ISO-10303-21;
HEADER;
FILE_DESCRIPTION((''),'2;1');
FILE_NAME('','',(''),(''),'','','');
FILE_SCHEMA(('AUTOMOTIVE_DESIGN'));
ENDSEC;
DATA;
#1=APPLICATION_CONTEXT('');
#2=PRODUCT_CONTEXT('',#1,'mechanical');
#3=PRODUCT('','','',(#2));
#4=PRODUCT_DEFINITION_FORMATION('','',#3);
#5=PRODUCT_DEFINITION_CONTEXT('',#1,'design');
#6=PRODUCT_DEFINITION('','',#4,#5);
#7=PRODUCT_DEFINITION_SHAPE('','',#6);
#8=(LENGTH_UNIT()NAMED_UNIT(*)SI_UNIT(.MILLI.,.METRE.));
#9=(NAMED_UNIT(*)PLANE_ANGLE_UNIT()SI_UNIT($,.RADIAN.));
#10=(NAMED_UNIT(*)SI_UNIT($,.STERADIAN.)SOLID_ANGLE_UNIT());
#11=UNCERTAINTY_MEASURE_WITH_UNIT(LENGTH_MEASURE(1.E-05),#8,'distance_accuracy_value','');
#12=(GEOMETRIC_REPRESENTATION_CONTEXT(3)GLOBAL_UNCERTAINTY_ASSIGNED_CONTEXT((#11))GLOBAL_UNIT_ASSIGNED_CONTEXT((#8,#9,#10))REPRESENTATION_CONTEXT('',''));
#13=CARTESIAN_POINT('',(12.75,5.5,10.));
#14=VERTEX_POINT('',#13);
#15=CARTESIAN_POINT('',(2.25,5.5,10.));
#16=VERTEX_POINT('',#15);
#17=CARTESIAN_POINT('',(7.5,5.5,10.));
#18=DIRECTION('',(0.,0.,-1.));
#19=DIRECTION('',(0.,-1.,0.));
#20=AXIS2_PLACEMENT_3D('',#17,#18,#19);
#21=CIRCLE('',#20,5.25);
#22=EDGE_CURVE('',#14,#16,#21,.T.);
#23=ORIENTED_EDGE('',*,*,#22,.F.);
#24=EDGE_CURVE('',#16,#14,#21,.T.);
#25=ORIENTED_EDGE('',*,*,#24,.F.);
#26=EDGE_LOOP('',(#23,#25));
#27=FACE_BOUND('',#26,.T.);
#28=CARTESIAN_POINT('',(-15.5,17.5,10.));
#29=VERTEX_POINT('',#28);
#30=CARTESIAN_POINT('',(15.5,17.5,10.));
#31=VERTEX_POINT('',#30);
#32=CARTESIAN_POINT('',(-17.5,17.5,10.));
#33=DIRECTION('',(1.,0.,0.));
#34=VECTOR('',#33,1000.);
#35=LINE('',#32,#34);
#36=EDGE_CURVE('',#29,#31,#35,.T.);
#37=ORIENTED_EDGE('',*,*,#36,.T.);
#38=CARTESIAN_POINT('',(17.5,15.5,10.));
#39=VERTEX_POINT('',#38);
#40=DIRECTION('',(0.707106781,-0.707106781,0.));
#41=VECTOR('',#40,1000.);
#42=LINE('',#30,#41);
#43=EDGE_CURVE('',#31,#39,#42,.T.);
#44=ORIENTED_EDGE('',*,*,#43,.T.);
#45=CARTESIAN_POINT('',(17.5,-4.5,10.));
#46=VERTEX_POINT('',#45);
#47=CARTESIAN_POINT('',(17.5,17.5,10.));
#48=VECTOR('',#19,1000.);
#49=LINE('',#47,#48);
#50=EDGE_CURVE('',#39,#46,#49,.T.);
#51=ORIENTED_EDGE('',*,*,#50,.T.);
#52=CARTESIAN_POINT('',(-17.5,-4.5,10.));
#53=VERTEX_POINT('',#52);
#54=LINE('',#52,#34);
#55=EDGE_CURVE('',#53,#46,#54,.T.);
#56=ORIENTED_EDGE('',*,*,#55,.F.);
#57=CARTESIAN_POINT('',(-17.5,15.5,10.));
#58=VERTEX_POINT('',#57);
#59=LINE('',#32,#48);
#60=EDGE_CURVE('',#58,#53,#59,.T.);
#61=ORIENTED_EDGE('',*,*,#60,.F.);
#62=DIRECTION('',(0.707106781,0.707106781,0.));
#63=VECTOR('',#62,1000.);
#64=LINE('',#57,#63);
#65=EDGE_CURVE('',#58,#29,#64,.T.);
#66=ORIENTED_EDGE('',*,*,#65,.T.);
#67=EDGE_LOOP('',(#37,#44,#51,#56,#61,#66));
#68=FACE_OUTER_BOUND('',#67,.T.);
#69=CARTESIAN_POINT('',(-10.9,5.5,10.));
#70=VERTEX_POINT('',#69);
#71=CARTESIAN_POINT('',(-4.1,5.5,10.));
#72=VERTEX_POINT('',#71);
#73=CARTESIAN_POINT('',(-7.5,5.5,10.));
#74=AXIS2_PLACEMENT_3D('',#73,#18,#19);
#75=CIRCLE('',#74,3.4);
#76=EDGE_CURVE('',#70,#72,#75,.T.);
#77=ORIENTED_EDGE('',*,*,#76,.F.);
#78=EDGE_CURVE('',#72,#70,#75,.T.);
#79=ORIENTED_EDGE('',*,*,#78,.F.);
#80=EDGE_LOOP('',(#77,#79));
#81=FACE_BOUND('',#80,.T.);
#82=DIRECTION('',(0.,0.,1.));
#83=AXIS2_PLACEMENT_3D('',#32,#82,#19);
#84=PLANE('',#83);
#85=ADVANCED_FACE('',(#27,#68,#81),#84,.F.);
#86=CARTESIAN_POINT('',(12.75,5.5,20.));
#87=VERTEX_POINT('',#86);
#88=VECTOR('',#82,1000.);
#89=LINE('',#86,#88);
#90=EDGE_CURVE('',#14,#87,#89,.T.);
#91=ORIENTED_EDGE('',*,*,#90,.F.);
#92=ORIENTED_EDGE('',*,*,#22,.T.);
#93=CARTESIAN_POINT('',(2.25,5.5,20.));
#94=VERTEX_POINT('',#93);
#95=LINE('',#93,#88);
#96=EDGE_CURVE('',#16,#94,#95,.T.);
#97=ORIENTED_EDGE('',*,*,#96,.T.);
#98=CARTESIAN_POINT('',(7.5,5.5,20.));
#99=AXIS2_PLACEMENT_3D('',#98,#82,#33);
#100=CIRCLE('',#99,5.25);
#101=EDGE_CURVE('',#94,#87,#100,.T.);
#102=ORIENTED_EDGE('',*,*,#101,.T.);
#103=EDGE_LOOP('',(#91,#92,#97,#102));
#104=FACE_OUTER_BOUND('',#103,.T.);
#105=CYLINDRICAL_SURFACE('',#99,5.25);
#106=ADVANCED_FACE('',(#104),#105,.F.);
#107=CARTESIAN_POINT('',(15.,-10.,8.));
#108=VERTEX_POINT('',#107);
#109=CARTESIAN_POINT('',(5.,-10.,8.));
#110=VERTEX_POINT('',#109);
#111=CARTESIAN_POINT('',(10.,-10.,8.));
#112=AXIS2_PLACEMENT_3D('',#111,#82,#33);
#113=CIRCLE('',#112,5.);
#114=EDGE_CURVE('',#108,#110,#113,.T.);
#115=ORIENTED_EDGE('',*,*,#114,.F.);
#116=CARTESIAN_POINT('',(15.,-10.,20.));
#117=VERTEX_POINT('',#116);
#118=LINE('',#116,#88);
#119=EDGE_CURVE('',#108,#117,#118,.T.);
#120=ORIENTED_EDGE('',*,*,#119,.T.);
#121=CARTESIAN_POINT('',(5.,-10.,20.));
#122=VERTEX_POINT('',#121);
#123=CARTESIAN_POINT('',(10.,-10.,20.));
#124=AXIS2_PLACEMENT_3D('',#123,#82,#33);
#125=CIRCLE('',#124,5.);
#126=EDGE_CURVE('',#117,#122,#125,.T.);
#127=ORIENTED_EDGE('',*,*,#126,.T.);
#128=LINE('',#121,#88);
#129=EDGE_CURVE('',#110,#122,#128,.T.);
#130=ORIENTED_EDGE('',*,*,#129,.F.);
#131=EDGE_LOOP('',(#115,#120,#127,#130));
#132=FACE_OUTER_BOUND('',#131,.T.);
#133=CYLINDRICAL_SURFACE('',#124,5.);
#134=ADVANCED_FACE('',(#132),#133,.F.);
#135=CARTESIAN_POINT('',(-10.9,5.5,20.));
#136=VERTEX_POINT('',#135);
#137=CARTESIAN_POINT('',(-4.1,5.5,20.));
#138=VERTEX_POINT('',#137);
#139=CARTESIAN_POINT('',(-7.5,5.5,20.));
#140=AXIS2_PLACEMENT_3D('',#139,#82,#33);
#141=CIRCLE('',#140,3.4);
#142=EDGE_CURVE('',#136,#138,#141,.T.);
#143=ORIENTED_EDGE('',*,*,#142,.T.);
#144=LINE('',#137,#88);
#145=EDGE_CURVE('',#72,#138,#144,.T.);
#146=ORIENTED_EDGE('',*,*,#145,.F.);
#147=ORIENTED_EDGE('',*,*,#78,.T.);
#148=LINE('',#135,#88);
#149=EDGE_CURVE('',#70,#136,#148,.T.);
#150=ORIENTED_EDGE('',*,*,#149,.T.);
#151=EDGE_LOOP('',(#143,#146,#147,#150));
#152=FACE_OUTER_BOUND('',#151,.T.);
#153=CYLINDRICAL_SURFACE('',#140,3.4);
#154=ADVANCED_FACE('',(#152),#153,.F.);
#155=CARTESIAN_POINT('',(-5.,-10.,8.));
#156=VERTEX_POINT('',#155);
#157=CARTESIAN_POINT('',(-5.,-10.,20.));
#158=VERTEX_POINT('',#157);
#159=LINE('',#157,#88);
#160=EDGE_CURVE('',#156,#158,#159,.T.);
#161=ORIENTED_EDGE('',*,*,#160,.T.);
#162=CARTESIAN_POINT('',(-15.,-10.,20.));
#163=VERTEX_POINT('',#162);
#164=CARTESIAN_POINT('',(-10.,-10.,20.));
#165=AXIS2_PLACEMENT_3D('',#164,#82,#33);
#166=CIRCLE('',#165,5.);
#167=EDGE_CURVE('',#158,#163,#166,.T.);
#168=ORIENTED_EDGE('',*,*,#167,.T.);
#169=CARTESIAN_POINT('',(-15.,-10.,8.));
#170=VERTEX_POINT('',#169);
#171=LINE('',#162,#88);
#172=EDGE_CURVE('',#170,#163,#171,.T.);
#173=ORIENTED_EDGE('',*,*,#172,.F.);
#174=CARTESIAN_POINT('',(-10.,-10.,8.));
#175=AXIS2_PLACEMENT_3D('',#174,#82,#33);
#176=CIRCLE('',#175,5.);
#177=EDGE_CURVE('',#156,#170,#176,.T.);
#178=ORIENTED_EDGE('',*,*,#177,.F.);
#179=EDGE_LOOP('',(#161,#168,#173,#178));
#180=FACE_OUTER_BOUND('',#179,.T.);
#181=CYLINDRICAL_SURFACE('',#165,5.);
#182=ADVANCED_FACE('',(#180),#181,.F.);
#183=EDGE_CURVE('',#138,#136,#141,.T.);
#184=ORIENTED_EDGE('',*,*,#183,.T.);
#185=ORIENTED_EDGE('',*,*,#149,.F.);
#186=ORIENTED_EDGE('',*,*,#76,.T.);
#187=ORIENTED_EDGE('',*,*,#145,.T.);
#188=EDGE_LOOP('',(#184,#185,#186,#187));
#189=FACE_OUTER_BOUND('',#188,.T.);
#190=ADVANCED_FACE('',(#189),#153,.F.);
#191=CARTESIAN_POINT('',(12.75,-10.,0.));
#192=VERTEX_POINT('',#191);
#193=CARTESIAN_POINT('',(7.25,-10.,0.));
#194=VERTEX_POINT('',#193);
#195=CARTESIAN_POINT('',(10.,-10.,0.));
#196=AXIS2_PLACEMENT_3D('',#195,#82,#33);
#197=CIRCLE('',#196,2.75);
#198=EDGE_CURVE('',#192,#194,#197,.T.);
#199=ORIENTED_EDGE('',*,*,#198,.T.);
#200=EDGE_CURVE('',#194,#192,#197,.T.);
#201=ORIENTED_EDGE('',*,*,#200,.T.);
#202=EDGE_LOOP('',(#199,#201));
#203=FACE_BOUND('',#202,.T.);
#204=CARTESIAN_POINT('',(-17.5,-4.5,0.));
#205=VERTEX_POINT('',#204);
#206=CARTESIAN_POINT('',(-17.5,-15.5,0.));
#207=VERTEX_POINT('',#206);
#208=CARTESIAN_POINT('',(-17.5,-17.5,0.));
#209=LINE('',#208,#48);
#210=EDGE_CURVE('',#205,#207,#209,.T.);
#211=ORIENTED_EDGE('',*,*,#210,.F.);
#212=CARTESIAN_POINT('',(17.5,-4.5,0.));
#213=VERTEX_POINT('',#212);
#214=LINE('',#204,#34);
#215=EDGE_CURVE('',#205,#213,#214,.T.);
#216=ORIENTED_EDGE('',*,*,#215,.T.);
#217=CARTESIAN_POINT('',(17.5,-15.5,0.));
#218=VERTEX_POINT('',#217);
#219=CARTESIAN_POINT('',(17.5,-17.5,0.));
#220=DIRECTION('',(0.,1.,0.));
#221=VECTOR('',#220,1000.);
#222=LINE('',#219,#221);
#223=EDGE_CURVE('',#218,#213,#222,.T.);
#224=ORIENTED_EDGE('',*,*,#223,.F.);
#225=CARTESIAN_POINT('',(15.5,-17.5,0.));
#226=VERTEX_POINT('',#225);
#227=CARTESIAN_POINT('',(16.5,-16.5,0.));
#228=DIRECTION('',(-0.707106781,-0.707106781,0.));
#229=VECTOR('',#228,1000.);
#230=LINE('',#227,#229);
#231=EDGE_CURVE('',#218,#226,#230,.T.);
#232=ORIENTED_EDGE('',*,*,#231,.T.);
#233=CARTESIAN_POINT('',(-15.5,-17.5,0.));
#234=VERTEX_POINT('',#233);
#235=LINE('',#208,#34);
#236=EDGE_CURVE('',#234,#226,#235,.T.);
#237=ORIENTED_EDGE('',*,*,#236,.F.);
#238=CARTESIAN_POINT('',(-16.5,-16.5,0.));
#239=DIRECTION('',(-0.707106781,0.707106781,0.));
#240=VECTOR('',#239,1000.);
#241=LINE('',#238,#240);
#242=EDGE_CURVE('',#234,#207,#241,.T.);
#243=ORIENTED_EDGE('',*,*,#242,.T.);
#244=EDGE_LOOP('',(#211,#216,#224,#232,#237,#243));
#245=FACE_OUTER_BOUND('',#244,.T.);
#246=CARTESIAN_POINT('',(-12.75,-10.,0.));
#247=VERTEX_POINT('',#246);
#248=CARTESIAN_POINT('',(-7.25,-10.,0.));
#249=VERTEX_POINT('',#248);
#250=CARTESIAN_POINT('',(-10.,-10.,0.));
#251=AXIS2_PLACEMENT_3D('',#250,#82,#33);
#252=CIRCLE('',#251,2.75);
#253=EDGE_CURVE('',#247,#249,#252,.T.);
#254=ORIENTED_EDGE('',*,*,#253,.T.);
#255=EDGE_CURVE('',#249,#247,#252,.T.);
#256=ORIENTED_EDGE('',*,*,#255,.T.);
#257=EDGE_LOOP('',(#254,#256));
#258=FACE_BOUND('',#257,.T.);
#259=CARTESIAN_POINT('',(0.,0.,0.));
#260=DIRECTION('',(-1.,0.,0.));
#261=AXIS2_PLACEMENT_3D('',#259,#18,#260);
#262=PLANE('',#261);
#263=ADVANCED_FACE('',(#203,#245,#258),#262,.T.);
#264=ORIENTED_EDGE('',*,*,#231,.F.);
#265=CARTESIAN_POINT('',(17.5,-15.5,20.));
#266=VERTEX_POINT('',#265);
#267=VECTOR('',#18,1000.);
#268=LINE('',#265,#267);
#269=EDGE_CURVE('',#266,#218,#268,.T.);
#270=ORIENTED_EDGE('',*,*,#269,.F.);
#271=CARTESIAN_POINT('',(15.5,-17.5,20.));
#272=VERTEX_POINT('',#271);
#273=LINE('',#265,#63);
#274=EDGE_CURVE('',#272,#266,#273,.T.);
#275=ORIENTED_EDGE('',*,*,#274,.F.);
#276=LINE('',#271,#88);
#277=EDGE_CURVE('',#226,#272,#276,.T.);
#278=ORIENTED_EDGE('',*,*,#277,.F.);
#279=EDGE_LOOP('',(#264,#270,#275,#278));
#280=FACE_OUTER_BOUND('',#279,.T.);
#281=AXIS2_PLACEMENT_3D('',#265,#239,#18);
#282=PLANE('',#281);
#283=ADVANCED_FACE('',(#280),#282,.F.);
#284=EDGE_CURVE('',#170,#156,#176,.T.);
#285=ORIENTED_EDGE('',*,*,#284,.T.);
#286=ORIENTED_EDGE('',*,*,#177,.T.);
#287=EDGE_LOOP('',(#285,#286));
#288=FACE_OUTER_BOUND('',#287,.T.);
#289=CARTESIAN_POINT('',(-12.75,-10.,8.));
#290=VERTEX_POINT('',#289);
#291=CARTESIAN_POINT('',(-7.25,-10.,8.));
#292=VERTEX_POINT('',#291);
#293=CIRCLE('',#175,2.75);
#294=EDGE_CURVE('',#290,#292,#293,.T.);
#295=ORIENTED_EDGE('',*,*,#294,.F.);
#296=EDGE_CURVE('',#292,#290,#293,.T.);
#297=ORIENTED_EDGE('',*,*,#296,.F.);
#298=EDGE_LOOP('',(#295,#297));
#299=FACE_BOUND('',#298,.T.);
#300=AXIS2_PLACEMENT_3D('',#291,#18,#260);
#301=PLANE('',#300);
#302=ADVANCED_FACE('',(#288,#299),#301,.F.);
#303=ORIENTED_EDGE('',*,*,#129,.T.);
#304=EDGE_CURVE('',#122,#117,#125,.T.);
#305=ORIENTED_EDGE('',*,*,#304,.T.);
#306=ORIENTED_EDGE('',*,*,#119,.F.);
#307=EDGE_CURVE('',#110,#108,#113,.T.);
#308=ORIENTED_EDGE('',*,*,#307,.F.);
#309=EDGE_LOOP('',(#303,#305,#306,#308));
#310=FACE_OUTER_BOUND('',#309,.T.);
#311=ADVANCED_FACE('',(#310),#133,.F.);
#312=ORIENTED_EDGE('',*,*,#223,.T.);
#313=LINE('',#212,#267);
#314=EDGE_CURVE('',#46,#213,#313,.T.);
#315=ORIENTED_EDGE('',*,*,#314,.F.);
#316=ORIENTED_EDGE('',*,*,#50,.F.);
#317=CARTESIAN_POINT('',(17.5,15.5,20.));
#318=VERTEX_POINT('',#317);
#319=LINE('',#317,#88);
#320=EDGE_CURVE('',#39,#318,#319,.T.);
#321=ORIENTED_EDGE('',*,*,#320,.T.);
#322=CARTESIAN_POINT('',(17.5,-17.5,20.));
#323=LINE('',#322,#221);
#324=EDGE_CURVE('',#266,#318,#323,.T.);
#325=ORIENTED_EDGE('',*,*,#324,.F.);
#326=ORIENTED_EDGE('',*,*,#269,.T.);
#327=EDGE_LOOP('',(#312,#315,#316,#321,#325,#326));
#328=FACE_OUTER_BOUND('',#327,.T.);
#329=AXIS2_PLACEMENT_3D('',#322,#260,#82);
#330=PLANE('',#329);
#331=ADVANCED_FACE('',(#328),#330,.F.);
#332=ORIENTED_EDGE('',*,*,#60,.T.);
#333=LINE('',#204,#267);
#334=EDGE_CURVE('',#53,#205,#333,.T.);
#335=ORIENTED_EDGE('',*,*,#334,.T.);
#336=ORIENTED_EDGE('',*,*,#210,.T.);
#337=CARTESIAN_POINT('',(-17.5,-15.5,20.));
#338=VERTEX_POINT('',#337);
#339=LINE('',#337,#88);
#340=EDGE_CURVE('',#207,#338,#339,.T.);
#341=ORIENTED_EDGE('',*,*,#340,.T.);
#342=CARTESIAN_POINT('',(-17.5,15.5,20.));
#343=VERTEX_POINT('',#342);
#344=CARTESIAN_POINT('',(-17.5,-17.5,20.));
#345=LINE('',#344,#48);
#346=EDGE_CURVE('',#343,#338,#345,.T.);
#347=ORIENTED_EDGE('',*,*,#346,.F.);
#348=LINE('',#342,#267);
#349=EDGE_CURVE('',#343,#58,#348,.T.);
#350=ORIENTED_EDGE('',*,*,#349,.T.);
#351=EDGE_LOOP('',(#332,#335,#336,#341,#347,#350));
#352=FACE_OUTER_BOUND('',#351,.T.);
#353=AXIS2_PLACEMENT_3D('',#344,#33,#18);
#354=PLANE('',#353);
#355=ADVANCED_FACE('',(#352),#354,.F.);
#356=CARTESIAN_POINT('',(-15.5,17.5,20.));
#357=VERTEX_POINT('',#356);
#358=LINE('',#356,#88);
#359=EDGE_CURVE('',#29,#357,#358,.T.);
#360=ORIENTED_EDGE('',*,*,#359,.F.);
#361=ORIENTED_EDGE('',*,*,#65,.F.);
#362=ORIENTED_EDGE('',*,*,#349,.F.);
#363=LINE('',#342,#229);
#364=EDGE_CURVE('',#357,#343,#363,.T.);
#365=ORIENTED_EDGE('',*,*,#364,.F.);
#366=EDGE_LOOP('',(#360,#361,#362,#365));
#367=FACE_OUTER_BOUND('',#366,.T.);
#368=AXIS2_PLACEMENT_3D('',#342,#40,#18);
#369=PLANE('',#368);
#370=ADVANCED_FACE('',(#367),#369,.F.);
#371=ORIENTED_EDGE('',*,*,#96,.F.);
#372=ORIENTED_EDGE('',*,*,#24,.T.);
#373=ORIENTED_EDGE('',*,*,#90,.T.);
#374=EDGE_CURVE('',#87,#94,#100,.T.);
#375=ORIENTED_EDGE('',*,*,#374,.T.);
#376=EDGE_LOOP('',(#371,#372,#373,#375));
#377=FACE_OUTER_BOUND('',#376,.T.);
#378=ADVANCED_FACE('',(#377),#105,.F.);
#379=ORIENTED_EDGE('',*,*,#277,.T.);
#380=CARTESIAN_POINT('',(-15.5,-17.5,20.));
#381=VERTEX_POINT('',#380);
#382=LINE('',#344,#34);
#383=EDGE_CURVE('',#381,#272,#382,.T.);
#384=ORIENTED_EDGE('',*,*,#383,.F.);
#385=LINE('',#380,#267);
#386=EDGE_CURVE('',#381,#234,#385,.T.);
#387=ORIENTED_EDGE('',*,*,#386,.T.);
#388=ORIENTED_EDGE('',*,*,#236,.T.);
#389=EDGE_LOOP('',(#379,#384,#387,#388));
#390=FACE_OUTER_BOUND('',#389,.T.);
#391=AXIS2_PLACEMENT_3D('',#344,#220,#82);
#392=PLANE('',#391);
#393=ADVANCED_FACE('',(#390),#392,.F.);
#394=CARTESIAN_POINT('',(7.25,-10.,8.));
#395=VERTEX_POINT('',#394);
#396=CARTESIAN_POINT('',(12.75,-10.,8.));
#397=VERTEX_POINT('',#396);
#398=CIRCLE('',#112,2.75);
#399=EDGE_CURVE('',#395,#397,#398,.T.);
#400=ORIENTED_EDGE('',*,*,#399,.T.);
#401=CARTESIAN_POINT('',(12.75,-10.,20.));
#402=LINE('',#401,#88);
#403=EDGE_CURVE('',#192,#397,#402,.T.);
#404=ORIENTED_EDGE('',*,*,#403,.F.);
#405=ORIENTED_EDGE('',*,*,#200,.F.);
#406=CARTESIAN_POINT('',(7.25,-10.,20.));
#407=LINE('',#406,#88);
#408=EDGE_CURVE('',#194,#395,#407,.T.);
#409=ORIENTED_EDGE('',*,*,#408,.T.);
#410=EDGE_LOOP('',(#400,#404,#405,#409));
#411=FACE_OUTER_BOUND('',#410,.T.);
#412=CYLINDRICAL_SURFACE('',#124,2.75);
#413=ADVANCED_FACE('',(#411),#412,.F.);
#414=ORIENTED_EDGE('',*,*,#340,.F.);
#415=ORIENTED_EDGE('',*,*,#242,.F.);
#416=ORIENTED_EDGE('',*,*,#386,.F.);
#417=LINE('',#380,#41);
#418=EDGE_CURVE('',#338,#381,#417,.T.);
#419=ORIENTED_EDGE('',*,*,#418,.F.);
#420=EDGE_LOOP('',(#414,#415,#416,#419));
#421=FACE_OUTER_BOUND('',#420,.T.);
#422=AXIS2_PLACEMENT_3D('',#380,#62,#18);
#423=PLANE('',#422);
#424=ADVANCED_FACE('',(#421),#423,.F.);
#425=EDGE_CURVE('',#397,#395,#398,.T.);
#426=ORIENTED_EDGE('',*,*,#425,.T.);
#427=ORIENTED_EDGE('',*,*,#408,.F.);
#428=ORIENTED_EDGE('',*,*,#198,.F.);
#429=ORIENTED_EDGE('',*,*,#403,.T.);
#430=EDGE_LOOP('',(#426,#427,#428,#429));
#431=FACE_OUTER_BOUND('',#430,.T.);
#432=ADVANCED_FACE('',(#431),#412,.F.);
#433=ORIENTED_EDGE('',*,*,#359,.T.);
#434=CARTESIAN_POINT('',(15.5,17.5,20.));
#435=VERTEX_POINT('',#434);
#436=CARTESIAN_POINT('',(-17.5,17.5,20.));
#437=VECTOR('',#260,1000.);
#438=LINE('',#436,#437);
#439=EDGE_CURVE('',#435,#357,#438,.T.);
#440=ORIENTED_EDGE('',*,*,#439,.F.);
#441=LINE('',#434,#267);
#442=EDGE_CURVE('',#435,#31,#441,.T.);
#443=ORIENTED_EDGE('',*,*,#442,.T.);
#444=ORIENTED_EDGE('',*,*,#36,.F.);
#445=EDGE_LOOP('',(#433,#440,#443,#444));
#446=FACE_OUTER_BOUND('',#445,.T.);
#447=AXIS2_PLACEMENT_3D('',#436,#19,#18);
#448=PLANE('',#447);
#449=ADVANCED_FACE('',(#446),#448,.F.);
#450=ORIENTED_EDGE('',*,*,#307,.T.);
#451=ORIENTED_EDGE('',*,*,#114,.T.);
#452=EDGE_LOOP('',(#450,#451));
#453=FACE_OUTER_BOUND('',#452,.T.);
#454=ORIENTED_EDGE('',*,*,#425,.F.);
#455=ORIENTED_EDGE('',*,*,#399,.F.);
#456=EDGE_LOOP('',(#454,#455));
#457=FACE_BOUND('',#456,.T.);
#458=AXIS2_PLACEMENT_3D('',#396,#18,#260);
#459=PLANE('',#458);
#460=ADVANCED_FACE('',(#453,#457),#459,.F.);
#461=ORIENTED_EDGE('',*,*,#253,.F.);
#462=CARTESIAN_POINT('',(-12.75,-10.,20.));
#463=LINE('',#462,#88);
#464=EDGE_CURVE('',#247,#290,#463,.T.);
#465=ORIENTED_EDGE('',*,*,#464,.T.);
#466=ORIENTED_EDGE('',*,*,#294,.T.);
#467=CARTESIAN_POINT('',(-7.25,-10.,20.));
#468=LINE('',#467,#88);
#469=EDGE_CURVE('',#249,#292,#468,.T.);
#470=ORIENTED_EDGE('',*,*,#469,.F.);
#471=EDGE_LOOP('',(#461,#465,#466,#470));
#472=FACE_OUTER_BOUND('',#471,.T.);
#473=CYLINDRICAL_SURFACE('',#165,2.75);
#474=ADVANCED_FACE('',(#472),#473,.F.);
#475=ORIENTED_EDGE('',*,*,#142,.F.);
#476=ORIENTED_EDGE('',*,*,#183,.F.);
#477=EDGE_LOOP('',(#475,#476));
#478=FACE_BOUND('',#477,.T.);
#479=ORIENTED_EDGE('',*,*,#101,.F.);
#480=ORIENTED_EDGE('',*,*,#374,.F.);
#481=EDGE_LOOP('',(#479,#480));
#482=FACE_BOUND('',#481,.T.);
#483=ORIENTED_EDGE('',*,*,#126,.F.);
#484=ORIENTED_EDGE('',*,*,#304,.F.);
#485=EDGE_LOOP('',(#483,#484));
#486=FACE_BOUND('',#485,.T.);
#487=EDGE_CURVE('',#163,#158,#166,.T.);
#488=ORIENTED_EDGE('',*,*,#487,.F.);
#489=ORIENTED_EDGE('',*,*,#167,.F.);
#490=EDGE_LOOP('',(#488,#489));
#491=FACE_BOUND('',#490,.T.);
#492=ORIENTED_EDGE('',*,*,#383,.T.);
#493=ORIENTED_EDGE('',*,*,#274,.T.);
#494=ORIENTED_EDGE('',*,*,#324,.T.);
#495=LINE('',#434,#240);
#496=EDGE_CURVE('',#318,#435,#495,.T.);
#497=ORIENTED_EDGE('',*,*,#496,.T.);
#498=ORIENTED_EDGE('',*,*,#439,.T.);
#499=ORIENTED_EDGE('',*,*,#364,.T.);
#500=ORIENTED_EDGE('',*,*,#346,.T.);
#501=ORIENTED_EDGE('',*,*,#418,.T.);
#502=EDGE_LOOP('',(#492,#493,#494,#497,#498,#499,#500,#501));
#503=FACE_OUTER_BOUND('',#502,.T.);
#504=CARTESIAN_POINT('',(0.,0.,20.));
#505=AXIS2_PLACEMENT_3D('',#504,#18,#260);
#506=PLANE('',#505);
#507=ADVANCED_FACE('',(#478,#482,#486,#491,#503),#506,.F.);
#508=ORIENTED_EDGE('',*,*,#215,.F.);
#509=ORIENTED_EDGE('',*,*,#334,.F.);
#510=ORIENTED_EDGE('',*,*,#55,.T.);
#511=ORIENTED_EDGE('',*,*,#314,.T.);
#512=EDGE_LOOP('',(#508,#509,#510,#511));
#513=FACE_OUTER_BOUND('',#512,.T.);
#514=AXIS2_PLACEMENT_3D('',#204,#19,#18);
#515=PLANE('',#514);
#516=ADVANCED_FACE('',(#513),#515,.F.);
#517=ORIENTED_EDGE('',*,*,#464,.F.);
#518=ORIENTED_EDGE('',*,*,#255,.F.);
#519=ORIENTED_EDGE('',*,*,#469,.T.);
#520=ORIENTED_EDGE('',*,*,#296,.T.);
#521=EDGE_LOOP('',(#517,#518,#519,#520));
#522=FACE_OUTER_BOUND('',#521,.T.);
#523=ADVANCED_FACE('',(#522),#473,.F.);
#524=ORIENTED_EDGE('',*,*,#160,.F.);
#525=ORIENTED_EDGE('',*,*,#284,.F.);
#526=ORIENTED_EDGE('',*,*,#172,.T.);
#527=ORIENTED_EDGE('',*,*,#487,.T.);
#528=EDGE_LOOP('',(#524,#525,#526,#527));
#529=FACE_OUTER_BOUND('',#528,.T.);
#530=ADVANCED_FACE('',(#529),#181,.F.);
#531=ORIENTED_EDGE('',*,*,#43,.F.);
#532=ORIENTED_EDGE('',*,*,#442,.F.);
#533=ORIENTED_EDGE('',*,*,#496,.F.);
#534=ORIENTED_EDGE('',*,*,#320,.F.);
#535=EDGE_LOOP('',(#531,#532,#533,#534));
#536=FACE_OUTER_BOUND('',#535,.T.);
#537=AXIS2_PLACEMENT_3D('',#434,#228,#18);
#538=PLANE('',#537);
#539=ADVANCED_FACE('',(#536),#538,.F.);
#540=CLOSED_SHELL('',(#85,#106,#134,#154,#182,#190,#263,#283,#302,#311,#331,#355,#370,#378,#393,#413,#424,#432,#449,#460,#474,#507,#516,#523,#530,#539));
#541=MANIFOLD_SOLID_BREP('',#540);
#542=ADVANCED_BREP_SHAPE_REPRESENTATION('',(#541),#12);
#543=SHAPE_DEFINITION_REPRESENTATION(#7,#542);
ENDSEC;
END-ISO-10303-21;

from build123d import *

# Parameters (mm, degrees)
SKETCH_1_W                   = 35
SKETCH_1_H                   = 35
EXTRUDE_1_DEPTH              = 20
CHAMFER_1_SIZE               = 2
M12X1_25_1_D                 = 10.5
HOLE_WIZARD_M8_1_D           = 6.8
HOLE_WIZARD_M5_1_D           = 5.5
HOLE_WIZARD_M5_1_CBORE_D     = 10
HOLE_WIZARD_M5_1_CBORE_DEPTH = 12
SKETCH_11_W                  = 10
SKETCH_11_H                  = 22
CUT_EXTRUDE_1_DEPTH          = 44.945989578


with BuildPart() as part:
    # 草图1 → 凸台-拉伸1 (new body)
    with BuildSketch(Plane.XY):
        Rectangle(SKETCH_1_W, SKETCH_1_H)
    extrude(amount=EXTRUDE_1_DEPTH)

    # 倒角1
    chamfer_1_edges = [part.edges().sort_by_distance(p)[0] for p in [
        (17.5, -17.5, 10),
        (-17.5, -17.5, 10),
        (-17.5, 17.5, 10),
        (17.5, 17.5, 10),
    ]]
    chamfer(chamfer_1_edges, length=CHAMFER_1_SIZE)

    # M12x1.25 螺纹孔1 (through all)
    with Locations(Plane.XY.offset(20)):
        with Locations((7.5, 5.5)):
            Hole(M12X1_25_1_D / 2)

    # M8 螺纹孔1 (through all)
    with Locations(Plane.XY.offset(20)):
        with Locations((-7.5, 5.5)):
            Hole(HOLE_WIZARD_M8_1_D / 2)

    # M5 六角圆柱头螺钉的柱形沉头孔1 (through all)
    with Locations(Plane.XY.offset(20)):
        with Locations((-10, -10), (10, -10)):
            CounterBoreHole(HOLE_WIZARD_M5_1_D / 2, HOLE_WIZARD_M5_1_CBORE_D / 2, HOLE_WIZARD_M5_1_CBORE_DEPTH)

    # 草图11 → 切除-拉伸1 (cut, through all)
    with BuildSketch(Plane(origin=(17.5, 0, 0), x_dir=(0, 0, -1), z_dir=(1, 0, 0))):
        with Locations((-5, 6.5)):
            Rectangle(SKETCH_11_W, SKETCH_11_H)
    extrude(amount=-CUT_EXTRUDE_1_DEPTH, mode=Mode.SUBTRACT)


solid = part.part
